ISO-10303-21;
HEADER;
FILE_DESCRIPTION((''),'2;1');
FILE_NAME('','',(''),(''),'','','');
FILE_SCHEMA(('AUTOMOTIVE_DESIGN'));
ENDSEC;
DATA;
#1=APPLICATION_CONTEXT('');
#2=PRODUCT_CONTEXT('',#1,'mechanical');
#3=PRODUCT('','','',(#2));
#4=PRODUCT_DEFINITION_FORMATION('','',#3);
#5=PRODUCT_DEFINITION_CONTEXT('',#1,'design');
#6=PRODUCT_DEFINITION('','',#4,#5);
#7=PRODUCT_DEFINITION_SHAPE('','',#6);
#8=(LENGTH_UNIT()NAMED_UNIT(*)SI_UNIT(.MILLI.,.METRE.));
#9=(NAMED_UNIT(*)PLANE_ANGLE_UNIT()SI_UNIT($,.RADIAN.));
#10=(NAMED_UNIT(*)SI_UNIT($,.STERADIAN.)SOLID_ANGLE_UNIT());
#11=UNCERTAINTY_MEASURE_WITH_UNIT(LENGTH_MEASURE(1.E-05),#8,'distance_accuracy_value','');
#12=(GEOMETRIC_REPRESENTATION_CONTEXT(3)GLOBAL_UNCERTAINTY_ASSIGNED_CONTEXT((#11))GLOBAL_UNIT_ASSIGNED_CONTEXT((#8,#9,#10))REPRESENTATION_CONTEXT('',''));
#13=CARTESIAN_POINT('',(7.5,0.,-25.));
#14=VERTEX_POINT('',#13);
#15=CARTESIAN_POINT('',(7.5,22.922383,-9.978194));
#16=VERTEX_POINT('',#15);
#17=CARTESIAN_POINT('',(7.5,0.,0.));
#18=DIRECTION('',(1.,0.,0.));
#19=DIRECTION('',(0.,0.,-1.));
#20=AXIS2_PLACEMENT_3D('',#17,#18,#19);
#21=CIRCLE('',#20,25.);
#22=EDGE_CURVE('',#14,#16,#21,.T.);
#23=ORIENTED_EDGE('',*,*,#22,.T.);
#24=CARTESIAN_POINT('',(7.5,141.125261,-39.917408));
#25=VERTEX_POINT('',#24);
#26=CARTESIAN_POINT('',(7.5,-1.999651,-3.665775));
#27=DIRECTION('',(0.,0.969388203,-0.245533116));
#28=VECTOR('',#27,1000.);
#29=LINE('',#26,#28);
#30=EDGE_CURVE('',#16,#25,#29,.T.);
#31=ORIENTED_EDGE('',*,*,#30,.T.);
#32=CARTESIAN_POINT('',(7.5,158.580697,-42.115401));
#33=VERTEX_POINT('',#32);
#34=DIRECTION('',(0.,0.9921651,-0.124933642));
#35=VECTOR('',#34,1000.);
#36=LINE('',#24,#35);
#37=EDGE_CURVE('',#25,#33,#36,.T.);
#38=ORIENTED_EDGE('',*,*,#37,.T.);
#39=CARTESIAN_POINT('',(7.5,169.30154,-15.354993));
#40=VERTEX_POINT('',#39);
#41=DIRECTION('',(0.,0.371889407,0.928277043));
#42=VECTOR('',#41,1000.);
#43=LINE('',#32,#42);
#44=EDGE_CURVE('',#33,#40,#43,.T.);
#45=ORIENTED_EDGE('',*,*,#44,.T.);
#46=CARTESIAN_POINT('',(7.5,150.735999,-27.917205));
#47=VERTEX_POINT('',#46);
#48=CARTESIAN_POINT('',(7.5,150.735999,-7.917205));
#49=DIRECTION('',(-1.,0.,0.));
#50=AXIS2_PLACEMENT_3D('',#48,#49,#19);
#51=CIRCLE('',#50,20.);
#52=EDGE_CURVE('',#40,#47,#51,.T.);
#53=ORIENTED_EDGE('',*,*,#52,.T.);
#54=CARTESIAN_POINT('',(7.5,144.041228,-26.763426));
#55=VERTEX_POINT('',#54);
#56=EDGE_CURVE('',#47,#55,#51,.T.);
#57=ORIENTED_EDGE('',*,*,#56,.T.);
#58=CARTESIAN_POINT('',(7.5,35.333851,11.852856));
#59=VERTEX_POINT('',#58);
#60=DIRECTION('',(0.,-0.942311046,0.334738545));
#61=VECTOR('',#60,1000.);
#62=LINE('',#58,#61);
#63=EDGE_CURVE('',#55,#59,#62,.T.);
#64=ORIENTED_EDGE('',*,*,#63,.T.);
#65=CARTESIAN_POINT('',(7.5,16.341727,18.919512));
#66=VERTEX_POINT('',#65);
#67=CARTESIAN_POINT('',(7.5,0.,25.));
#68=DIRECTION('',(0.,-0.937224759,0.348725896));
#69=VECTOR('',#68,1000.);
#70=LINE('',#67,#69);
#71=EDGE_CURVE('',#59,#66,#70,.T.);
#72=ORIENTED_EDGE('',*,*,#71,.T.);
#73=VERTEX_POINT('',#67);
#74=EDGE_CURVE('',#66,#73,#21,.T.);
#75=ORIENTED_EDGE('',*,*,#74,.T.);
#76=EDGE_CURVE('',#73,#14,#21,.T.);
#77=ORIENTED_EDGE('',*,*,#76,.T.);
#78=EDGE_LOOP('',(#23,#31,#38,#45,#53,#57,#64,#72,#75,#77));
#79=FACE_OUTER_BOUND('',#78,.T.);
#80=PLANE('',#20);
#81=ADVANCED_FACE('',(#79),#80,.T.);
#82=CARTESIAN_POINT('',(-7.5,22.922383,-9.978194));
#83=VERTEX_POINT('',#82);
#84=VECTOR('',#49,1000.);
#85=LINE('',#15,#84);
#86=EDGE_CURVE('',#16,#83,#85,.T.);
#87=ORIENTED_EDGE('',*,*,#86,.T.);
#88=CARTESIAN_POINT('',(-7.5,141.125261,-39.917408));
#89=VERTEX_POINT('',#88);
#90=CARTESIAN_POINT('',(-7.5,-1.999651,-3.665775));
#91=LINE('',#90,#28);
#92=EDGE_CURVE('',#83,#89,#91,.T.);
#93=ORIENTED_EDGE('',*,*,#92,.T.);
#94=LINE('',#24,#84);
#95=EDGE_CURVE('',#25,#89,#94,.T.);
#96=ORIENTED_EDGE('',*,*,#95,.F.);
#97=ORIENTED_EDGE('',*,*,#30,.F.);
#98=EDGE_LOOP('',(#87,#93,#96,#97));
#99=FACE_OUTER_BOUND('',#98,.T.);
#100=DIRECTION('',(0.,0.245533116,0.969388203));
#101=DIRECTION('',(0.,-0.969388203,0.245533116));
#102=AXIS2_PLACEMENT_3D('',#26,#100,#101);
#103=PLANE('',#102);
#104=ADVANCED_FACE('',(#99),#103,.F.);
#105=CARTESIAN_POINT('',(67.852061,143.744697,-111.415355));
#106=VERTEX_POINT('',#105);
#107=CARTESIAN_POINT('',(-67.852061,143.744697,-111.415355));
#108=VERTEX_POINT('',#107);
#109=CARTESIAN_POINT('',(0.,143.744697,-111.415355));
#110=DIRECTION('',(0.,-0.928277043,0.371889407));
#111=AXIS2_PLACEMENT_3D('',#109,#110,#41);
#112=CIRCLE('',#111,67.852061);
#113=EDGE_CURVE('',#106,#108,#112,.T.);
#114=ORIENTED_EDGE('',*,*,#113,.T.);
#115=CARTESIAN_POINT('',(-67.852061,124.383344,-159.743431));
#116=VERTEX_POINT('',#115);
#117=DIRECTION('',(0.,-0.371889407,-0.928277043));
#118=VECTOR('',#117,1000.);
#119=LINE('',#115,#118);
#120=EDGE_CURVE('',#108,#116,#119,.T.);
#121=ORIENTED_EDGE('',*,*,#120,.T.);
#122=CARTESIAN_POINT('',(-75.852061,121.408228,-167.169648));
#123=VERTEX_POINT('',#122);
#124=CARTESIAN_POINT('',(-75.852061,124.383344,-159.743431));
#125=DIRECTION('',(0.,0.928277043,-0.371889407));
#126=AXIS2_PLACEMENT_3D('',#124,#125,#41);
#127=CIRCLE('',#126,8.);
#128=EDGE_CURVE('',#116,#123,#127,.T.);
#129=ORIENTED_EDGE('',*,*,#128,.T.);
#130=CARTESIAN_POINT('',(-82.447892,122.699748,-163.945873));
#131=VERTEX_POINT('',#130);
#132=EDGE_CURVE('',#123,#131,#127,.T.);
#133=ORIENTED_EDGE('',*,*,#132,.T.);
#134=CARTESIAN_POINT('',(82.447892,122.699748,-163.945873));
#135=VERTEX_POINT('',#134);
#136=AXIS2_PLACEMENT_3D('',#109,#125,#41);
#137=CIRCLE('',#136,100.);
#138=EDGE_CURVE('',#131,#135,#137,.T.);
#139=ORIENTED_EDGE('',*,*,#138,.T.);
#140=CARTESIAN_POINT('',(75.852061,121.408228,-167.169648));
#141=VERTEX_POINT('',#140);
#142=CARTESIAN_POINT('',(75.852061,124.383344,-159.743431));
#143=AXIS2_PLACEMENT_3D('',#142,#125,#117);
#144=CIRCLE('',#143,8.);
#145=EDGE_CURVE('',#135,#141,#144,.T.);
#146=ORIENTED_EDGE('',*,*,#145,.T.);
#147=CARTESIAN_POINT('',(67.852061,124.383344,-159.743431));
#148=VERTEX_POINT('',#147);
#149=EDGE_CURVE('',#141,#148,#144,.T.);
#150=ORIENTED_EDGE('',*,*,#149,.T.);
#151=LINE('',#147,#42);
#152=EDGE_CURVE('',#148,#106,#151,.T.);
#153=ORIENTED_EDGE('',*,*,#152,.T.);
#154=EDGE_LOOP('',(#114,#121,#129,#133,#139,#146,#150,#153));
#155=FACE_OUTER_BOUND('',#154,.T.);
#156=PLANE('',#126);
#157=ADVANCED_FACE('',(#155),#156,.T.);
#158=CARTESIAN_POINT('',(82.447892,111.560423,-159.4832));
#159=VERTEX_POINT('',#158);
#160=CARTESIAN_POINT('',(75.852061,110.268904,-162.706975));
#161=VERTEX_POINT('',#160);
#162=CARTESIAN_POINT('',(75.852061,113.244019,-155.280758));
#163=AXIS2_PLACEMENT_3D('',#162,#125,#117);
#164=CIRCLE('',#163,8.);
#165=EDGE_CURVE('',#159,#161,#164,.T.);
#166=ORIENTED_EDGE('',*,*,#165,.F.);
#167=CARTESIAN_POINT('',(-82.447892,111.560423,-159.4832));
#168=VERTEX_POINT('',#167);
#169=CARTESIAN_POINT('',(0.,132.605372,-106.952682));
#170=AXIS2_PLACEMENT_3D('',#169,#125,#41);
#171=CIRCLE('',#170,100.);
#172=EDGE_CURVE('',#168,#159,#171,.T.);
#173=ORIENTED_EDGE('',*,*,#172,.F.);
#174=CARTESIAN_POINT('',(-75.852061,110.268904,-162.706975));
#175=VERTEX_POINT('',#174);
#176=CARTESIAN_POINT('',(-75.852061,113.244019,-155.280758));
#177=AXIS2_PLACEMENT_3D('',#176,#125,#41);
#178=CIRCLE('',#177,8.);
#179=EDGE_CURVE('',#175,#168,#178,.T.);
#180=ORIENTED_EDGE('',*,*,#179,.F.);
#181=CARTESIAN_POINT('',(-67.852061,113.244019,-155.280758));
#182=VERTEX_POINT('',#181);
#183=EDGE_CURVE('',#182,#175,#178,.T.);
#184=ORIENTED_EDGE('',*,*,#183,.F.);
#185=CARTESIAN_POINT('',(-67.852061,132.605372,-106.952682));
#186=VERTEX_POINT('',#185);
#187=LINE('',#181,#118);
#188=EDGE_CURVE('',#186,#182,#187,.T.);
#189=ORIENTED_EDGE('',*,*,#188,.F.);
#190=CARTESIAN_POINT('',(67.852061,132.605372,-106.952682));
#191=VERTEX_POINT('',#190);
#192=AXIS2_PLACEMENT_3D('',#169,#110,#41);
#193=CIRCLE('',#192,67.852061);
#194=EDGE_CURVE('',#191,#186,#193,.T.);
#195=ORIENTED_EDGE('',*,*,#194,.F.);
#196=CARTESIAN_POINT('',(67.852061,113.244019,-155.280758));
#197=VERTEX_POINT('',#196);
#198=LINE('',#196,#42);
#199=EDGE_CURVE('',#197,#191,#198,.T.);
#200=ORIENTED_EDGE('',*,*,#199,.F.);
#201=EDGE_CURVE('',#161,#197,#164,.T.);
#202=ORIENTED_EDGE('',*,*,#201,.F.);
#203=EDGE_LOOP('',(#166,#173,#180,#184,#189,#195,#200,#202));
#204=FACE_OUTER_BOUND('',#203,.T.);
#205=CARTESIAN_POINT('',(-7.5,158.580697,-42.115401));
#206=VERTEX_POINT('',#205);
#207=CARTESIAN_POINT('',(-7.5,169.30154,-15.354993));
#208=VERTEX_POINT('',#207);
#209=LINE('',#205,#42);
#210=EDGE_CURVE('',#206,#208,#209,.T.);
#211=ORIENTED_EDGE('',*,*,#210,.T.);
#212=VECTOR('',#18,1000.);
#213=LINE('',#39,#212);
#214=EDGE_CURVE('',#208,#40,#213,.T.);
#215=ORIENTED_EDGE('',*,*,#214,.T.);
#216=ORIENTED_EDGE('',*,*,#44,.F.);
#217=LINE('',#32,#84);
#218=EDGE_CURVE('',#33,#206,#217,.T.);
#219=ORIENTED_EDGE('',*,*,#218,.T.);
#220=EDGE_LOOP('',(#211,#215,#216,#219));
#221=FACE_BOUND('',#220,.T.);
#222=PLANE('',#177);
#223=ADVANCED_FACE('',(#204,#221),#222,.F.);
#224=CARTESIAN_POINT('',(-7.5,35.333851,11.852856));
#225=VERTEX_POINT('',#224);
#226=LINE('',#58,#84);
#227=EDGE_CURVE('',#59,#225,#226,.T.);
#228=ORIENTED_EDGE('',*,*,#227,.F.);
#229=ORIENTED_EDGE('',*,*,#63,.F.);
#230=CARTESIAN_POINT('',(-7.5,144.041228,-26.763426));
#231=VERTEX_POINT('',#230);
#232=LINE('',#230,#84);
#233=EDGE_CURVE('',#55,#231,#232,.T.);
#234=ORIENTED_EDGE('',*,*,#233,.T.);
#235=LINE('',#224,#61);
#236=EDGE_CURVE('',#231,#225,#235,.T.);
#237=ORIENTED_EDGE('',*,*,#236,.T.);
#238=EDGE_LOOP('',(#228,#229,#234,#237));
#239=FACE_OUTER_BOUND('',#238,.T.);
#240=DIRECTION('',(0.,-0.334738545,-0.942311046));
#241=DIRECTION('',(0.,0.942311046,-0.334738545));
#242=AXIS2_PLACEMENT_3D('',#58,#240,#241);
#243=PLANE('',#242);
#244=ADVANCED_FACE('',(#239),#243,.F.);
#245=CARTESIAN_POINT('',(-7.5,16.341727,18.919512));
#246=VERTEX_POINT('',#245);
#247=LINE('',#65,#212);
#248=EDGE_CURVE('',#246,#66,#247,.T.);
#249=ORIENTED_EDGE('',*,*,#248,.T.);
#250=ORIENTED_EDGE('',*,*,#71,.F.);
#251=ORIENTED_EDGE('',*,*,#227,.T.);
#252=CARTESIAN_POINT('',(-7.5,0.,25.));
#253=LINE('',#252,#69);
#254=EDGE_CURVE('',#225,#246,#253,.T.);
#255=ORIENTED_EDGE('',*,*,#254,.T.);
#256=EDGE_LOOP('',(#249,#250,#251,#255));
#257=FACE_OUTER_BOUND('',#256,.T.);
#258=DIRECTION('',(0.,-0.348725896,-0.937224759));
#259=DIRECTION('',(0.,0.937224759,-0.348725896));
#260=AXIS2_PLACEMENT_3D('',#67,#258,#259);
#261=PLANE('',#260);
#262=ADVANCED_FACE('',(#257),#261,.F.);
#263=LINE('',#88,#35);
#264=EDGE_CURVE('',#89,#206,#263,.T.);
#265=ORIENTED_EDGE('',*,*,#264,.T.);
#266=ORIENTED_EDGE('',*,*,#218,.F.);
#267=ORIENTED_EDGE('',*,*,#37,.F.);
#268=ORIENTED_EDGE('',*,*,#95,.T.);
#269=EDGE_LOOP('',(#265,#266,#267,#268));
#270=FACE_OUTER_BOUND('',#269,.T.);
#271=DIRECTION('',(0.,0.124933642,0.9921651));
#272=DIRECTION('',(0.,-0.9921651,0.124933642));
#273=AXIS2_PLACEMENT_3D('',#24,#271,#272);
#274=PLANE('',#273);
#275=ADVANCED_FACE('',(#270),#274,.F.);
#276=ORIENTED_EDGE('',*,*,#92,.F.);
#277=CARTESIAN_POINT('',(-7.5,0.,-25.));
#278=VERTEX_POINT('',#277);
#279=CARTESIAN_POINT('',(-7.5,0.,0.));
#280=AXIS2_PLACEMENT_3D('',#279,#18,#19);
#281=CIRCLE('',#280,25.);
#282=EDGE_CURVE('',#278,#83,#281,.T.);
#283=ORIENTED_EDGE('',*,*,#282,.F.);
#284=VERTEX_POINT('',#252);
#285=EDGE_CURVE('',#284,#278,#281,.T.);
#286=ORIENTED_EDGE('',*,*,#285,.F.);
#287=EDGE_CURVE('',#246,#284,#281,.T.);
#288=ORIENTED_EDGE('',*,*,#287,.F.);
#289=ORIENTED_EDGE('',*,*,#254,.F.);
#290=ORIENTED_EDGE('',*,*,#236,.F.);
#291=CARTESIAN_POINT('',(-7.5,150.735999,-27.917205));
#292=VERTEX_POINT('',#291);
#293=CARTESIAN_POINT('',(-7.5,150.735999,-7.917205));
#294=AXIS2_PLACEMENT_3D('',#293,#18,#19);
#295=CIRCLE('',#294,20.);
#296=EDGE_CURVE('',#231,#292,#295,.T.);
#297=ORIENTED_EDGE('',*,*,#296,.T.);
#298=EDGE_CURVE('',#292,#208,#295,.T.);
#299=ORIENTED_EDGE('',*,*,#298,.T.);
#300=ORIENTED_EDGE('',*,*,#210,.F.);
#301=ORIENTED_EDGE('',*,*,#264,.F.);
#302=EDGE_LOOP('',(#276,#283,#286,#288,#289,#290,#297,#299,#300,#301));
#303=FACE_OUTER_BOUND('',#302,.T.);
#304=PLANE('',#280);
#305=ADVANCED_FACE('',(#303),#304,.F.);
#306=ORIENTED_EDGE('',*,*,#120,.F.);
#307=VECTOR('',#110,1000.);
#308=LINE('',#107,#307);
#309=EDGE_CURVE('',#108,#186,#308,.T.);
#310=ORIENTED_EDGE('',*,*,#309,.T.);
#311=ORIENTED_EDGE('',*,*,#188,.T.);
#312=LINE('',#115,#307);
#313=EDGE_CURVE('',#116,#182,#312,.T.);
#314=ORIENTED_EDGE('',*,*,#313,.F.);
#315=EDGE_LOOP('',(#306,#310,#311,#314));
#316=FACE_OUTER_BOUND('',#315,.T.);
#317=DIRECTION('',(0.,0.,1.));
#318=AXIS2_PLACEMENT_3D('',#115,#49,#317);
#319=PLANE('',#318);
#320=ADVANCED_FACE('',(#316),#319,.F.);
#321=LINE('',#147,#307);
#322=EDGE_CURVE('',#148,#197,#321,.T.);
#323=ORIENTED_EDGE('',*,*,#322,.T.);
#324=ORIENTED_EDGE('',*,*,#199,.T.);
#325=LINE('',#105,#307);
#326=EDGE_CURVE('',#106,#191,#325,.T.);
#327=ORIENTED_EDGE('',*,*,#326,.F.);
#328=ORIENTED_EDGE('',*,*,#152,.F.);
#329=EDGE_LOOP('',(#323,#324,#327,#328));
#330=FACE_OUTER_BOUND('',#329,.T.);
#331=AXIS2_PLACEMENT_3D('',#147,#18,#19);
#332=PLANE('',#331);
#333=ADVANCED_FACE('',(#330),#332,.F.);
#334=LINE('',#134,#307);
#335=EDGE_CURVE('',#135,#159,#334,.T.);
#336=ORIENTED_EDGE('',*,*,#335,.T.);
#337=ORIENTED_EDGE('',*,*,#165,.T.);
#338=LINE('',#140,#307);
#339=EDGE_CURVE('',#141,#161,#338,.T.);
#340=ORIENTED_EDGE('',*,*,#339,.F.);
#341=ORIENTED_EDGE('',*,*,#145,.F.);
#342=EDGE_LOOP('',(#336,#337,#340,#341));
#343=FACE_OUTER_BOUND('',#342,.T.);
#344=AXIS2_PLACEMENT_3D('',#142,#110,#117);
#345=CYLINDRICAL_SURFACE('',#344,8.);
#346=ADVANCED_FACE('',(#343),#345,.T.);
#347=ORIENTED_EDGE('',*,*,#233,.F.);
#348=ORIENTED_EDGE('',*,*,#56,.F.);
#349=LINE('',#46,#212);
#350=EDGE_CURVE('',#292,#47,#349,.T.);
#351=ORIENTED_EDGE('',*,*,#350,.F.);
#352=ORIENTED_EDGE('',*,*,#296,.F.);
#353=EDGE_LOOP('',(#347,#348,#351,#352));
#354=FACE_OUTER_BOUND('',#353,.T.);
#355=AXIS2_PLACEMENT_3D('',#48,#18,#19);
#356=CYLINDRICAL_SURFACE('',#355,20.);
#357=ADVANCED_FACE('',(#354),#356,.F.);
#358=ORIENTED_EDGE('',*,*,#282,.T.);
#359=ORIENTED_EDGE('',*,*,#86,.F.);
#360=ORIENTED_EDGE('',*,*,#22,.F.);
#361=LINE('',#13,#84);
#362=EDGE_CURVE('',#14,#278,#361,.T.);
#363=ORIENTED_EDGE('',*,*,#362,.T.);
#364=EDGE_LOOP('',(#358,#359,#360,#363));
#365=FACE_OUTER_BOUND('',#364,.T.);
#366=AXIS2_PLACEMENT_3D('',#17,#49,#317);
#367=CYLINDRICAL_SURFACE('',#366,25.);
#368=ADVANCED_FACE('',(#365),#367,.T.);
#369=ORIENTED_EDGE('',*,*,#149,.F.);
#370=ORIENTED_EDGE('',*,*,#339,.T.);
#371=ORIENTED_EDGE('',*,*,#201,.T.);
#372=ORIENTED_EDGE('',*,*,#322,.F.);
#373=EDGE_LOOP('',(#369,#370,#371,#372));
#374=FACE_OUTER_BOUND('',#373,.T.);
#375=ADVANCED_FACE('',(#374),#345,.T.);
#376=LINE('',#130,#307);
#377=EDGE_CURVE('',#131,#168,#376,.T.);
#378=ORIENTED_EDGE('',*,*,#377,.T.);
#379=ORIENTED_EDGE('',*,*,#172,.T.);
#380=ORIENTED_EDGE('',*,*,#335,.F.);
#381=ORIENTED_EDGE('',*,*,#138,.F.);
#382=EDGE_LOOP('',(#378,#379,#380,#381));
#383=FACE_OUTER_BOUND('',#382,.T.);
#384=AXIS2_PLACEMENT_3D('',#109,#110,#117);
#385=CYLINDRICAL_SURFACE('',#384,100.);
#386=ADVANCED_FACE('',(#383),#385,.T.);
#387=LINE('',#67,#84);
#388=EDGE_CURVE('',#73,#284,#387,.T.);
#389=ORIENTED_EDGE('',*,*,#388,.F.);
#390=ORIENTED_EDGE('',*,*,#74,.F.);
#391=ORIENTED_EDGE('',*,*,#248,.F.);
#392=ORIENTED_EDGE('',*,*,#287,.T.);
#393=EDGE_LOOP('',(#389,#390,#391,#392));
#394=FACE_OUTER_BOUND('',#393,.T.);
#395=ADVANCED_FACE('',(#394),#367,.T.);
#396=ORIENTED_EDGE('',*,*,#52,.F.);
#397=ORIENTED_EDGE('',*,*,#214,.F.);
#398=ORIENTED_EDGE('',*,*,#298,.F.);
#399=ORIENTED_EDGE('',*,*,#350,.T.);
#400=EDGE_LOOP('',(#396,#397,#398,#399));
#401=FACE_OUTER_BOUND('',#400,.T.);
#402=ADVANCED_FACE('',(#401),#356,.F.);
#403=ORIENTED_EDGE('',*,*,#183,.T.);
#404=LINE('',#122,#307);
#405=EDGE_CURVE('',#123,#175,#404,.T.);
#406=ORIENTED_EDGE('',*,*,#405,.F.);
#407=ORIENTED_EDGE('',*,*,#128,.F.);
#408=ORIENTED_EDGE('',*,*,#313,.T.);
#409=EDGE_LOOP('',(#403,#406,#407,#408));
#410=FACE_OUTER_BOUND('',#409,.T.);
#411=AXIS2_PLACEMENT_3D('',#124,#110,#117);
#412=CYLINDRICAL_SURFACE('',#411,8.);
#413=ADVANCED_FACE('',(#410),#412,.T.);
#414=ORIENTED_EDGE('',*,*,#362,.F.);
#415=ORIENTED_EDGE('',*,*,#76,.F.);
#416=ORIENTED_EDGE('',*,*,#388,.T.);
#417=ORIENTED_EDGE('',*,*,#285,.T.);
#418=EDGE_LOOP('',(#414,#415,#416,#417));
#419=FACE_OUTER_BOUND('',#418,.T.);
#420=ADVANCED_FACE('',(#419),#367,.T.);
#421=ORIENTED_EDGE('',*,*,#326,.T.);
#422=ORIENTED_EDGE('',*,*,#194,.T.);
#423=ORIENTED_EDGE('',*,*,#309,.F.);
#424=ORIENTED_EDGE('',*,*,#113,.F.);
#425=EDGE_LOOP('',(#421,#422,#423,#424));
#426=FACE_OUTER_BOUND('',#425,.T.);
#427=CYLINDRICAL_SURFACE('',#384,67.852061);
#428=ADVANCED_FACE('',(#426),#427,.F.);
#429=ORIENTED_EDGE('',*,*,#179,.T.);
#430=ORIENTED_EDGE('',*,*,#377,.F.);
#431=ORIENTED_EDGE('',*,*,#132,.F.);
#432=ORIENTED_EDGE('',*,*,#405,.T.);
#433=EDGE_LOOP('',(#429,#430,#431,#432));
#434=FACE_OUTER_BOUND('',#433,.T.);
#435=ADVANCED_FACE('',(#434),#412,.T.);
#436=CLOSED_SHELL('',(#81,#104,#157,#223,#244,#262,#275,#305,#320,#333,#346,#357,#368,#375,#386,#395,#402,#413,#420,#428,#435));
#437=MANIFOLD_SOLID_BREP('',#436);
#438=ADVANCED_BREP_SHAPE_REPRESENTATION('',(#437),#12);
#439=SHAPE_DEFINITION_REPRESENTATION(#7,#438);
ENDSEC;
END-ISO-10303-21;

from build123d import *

# Parameters (mm, degrees)
SKETCH1_R           = 25
BOSS_EXTRUDE1_DEPTH = 7.5
BOSS_EXTRUDE2_DEPTH = 7.5
BOSS_EXTRUDE4_DEPTH = 12
FILLET1_R           = 20


with BuildPart() as part:
    # Sketch1 → Boss-Extrude1 (new, symmetric)
    with BuildSketch(Plane(origin=(0, 0, 0), x_dir=(0, 0, -1), z_dir=(1, 0, 0))):
        Circle(SKETCH1_R)
    extrude(amount=BOSS_EXTRUDE1_DEPTH, both=True)

    # Sketch2 → Boss-Extrude2 (add, symmetric)
    with BuildSketch(Plane(origin=(0, 0, 0), x_dir=(0, 0, -1), z_dir=(1, 0, 0))):
        Polygon((-25, 0), (-11.852856042, 35.333850942), (33.197452276, 162.153435325), (42.115400597, 158.580697497), (39.917408227, 141.125260536), (3.66577496, -1.999651309), align=None)
    extrude(amount=BOSS_EXTRUDE2_DEPTH, both=True)

    # Sketch4 → Boss-Extrude4 (add)
    with BuildSketch(Plane(origin=(0, 151.187639508, -60.569290091), x_dir=(1, 0, 0), z_dir=(0, 0.9282770434137098, -0.3718894065056191))):
        with BuildLine():
            Line((67.852060571, 102.029312181), (67.852060571, 49.967186724))
            ThreePointArc((67.852060571, 49.967186724), (0, -17.884873847), (-67.852060571, 49.967186724))
            Line((-67.852060571, 49.967186724), (-67.852060571, 102.029312181))
            ThreePointArc((-67.852060571, 102.029312181), (-73.482108128, 109.670210388), (-82.447891925, 106.556453525))
            ThreePointArc((-82.447891925, 106.556453525), (0, -50.032813276), (82.447891925, 106.556453525))
            ThreePointArc((82.447891925, 106.556453525), (73.482108128, 109.670210388), (67.852060571, 102.029312181))
        make_face()
    extrude(amount=BOSS_EXTRUDE4_DEPTH)

    # Fillet1
    fillet1_edges = [part.edges().sort_by_distance(p)[0] for p in [
        (0, 162.153435325, -33.197452276),
    ]]
    fillet(fillet1_edges, radius=FILLET1_R)


solid = part.part
